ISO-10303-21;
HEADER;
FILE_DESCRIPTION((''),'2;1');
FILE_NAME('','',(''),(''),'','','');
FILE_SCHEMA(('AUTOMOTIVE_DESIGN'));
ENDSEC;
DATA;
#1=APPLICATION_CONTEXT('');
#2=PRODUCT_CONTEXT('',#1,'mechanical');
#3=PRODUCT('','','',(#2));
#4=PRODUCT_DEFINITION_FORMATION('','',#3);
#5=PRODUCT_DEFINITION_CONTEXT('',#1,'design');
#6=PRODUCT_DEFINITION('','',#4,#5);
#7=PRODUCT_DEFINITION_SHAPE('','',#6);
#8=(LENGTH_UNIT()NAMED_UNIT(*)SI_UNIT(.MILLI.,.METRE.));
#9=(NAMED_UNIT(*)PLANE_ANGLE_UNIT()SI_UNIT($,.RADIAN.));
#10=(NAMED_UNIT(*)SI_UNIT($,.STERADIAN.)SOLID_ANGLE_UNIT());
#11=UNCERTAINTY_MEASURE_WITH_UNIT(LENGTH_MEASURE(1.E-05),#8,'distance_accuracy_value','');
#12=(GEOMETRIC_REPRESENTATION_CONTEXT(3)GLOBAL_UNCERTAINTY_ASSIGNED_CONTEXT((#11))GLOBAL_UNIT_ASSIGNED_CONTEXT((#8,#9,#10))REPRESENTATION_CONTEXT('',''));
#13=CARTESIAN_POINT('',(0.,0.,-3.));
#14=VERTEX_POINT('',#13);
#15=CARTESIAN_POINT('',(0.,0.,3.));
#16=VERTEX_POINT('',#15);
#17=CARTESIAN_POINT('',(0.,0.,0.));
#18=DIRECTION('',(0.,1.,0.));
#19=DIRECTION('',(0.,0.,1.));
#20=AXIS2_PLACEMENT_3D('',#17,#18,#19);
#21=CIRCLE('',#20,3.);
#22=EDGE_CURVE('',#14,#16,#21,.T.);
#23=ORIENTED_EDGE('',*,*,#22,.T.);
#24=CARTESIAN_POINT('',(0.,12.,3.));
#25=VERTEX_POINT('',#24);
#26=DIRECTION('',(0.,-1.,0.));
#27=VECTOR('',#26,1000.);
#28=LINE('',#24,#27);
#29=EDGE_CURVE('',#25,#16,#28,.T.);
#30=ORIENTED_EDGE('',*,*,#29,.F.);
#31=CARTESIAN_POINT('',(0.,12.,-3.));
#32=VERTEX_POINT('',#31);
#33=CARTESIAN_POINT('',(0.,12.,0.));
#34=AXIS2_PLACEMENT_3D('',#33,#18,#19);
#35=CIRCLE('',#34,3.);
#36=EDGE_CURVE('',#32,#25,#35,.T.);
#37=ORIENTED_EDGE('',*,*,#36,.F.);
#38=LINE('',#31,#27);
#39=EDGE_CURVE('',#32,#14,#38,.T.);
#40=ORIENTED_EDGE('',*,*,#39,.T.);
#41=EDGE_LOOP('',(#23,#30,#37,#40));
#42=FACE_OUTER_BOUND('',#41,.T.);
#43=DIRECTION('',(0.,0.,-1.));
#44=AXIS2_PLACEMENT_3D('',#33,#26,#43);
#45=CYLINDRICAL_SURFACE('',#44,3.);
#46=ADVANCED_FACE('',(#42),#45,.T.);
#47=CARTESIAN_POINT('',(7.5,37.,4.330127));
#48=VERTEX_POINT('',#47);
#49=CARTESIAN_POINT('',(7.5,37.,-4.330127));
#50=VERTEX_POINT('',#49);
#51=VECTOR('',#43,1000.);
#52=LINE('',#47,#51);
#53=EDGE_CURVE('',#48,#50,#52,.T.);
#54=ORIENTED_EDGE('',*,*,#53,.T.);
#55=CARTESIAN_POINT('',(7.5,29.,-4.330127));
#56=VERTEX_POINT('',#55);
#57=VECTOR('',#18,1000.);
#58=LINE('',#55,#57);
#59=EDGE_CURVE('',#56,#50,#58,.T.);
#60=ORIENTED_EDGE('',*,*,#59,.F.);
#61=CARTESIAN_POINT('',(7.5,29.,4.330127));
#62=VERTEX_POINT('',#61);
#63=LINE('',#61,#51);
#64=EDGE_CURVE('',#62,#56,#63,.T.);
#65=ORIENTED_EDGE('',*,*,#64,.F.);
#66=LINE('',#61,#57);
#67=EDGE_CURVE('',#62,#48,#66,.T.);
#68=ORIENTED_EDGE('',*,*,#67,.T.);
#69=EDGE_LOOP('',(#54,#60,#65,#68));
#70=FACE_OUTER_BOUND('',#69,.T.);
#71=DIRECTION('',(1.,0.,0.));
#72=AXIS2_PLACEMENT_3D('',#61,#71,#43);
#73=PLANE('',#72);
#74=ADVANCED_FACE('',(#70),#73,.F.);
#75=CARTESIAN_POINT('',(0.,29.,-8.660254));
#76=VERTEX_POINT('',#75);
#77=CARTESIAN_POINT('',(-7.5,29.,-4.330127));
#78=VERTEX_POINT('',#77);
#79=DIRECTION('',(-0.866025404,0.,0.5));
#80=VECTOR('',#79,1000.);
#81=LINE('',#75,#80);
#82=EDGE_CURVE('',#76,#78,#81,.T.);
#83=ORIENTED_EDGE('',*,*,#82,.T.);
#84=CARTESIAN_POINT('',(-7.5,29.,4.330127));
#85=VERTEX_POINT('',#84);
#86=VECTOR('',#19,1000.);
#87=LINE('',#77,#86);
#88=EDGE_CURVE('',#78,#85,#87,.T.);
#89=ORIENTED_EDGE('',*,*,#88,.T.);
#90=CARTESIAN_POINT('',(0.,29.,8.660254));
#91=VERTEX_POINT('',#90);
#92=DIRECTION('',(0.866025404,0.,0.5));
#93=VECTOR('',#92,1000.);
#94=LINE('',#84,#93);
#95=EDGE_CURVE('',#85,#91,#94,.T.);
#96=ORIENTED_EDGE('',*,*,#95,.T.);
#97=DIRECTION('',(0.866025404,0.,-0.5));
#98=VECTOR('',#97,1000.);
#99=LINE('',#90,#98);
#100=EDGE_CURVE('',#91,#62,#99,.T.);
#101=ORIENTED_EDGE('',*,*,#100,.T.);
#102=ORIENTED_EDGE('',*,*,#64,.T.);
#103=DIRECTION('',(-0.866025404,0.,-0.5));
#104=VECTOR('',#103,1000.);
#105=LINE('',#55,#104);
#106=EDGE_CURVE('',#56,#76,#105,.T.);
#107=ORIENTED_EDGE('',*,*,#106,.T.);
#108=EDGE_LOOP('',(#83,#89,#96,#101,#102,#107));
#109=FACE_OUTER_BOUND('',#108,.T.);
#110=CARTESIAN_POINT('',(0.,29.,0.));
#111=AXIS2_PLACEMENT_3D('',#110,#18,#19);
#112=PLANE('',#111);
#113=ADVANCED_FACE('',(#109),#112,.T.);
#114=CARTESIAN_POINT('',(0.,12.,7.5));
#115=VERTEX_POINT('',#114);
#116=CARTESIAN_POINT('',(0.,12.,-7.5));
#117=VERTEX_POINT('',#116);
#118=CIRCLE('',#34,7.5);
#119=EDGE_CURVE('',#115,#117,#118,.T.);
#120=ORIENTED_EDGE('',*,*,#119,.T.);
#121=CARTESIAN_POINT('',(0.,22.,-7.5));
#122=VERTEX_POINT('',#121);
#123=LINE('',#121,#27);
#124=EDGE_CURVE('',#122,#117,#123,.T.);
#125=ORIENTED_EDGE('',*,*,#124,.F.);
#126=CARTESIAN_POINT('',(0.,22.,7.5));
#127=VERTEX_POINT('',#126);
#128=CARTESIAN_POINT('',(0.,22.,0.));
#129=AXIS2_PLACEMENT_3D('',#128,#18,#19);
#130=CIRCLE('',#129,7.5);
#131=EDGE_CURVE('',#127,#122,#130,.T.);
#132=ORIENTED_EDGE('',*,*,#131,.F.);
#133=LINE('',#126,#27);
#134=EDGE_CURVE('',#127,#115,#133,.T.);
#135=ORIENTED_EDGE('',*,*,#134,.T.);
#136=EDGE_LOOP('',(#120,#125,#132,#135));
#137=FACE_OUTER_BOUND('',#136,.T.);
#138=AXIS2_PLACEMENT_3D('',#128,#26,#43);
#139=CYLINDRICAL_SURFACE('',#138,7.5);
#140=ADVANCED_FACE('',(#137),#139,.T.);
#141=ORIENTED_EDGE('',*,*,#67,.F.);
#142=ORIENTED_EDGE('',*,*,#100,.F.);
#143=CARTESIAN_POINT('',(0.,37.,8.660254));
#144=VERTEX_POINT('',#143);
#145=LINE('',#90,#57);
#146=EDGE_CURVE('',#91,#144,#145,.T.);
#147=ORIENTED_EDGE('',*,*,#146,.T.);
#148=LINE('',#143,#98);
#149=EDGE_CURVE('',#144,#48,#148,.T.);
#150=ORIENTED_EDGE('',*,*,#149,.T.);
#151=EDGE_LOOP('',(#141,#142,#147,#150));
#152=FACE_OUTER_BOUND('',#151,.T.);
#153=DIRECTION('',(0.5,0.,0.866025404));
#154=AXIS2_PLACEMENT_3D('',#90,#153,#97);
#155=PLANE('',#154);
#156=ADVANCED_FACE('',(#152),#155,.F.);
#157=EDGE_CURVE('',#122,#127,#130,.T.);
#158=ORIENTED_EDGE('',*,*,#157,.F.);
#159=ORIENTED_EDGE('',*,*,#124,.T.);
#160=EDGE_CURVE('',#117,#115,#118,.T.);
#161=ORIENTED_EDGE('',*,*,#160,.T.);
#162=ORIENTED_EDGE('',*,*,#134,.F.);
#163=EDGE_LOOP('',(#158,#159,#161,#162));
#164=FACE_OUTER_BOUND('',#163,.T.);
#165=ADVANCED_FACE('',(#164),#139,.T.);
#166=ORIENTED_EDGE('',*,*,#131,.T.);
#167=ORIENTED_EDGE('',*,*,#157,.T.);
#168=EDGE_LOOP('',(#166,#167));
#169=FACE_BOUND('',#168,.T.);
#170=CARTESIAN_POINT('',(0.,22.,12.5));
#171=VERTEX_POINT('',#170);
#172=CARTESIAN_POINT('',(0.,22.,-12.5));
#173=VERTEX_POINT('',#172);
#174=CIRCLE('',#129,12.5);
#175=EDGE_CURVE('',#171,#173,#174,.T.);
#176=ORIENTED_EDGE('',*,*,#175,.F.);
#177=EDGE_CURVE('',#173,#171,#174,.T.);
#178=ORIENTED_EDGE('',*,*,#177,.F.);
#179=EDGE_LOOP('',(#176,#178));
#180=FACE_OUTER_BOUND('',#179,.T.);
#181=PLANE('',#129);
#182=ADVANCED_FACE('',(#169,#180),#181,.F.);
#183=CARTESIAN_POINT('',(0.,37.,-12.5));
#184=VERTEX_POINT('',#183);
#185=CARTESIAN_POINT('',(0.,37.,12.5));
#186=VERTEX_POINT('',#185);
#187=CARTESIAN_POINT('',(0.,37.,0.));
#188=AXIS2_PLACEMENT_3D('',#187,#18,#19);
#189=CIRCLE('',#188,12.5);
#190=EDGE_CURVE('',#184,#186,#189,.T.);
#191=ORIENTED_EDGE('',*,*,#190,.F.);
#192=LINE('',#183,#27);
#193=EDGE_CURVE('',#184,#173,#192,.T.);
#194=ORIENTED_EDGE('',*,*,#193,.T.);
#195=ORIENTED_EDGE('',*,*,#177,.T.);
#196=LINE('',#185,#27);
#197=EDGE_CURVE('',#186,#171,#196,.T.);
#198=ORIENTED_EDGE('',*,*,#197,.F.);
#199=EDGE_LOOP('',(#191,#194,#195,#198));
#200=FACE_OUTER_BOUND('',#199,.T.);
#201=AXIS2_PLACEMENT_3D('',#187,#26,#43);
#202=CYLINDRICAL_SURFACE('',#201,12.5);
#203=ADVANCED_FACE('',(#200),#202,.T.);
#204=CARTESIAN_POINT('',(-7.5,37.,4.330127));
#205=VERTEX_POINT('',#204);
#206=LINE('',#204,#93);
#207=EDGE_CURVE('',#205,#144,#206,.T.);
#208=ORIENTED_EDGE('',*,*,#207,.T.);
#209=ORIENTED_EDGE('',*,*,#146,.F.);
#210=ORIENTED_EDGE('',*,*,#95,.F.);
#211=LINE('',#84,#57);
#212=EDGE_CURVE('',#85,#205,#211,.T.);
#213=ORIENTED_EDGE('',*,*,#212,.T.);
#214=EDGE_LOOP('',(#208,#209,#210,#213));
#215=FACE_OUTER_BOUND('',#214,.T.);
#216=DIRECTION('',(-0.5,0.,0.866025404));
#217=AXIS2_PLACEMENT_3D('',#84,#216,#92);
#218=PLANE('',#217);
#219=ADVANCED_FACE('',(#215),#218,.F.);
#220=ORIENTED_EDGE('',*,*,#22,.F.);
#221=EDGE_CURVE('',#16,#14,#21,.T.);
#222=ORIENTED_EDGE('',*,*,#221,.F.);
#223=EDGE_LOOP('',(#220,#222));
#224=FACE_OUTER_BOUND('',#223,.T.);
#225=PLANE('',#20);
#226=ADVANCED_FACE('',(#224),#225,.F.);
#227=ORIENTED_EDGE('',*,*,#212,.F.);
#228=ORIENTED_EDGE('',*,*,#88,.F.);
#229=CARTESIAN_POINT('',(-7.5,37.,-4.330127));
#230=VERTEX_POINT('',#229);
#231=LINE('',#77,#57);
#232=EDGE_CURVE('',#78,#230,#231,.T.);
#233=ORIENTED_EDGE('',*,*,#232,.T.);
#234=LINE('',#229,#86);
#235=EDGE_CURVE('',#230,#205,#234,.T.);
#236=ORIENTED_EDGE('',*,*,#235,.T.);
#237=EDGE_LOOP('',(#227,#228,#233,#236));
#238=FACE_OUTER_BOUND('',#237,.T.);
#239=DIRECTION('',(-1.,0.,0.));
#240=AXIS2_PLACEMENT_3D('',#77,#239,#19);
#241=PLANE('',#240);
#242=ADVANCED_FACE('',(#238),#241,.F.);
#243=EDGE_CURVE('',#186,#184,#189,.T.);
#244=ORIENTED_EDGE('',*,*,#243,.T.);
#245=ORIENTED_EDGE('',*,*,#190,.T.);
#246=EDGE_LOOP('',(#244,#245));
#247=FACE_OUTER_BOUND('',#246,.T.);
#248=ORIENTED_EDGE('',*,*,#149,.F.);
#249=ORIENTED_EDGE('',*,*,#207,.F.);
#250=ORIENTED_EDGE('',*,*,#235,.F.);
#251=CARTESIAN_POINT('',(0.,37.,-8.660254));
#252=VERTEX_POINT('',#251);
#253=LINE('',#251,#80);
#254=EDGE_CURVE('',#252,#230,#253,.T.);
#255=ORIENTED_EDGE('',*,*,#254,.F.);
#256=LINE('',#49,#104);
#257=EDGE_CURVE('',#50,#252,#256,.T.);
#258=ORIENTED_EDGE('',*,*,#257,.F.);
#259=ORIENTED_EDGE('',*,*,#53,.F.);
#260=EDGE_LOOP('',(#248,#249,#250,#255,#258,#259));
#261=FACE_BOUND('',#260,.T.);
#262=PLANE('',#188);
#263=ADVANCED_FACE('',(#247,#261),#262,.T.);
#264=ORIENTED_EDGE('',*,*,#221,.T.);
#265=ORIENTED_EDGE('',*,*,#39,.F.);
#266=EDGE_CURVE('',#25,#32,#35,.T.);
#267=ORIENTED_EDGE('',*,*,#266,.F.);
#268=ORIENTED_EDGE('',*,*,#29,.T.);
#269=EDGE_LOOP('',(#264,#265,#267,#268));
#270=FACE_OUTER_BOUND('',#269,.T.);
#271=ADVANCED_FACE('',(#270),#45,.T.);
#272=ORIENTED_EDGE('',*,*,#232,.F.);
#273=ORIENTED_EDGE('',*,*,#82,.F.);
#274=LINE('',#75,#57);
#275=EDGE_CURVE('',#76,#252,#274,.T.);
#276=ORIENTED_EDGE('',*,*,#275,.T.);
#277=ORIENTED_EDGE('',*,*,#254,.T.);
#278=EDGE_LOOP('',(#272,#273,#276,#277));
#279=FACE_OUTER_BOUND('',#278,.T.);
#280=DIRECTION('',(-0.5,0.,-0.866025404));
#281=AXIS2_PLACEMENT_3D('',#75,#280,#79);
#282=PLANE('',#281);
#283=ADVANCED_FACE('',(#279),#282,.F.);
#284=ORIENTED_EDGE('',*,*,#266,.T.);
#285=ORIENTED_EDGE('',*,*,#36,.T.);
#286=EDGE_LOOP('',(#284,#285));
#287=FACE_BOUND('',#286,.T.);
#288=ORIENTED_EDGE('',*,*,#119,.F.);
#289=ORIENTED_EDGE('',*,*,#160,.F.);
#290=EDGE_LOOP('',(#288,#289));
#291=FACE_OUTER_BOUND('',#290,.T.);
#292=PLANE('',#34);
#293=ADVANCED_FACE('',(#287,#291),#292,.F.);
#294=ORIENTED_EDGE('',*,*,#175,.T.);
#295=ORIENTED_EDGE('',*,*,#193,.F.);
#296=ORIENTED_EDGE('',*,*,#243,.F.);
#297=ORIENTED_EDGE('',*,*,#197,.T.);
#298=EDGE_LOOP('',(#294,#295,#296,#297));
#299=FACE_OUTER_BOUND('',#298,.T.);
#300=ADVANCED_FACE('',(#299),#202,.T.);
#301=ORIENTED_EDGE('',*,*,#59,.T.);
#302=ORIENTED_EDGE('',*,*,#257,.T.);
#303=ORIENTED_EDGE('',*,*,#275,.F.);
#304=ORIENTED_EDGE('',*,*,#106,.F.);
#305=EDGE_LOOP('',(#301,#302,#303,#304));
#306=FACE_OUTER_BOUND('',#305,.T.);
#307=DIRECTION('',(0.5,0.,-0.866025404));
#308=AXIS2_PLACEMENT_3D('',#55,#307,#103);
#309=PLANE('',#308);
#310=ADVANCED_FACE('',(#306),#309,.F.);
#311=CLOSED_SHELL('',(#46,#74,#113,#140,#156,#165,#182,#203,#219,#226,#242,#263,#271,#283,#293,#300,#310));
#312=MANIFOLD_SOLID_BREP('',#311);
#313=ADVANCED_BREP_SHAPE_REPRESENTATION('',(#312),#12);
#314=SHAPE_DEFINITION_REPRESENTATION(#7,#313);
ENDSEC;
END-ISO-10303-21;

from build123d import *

# Parameters (mm, degrees)
SKETCH1_R           = 3
BOSS_EXTRUDE1_DEPTH = 12
SKETCH2_R           = 7.5
BOSS_EXTRUDE2_DEPTH = 10
SKETCH3_R           = 12.5
BOSS_EXTRUDE3_DEPTH = 15
CUT_EXTRUDE1_DEPTH  = 8


with BuildPart() as part:
    # Sketch1 → Boss-Extrude1 (new body)
    with BuildSketch(Plane(origin=(0, 0, 0), x_dir=(1, 0, 0), z_dir=(0, 1, 0))):
        with Locations(Location((0, 0, 0), (0, 0, 270))):
            Circle(SKETCH1_R)
    extrude(amount=BOSS_EXTRUDE1_DEPTH)

    # Sketch2 → Boss-Extrude2 (add)
    with BuildSketch(Plane(origin=(0, 12, 0), x_dir=(1, 0, 0), z_dir=(0, 1, 0))):
        with Locations(Location((0, 0, 0), (0, 0, 270))):
            Circle(SKETCH2_R)
    extrude(amount=BOSS_EXTRUDE2_DEPTH)

    # Sketch3 → Boss-Extrude3 (add)
    with BuildSketch(Plane(origin=(0, 22, 0), x_dir=(1, 0, 0), z_dir=(0, 1, 0))):
        with Locations(Location((0, 0, 0), (0, 0, 270))):
            Circle(SKETCH3_R)
    extrude(amount=BOSS_EXTRUDE3_DEPTH)

    # Sketch4 → Cut-Extrude1 (cut)
    with BuildSketch(Plane(origin=(0, 37, 0), x_dir=(1, 0, 0), z_dir=(0, 1, 0))):
        Polygon((0, 8.660254038), (-7.5, 4.330127019), (-7.5, -4.330127019), (0, -8.660254038), (7.5, -4.330127019), (7.5, 4.330127019), align=None)
    extrude(amount=-CUT_EXTRUDE1_DEPTH, mode=Mode.SUBTRACT)


solid = part.part
